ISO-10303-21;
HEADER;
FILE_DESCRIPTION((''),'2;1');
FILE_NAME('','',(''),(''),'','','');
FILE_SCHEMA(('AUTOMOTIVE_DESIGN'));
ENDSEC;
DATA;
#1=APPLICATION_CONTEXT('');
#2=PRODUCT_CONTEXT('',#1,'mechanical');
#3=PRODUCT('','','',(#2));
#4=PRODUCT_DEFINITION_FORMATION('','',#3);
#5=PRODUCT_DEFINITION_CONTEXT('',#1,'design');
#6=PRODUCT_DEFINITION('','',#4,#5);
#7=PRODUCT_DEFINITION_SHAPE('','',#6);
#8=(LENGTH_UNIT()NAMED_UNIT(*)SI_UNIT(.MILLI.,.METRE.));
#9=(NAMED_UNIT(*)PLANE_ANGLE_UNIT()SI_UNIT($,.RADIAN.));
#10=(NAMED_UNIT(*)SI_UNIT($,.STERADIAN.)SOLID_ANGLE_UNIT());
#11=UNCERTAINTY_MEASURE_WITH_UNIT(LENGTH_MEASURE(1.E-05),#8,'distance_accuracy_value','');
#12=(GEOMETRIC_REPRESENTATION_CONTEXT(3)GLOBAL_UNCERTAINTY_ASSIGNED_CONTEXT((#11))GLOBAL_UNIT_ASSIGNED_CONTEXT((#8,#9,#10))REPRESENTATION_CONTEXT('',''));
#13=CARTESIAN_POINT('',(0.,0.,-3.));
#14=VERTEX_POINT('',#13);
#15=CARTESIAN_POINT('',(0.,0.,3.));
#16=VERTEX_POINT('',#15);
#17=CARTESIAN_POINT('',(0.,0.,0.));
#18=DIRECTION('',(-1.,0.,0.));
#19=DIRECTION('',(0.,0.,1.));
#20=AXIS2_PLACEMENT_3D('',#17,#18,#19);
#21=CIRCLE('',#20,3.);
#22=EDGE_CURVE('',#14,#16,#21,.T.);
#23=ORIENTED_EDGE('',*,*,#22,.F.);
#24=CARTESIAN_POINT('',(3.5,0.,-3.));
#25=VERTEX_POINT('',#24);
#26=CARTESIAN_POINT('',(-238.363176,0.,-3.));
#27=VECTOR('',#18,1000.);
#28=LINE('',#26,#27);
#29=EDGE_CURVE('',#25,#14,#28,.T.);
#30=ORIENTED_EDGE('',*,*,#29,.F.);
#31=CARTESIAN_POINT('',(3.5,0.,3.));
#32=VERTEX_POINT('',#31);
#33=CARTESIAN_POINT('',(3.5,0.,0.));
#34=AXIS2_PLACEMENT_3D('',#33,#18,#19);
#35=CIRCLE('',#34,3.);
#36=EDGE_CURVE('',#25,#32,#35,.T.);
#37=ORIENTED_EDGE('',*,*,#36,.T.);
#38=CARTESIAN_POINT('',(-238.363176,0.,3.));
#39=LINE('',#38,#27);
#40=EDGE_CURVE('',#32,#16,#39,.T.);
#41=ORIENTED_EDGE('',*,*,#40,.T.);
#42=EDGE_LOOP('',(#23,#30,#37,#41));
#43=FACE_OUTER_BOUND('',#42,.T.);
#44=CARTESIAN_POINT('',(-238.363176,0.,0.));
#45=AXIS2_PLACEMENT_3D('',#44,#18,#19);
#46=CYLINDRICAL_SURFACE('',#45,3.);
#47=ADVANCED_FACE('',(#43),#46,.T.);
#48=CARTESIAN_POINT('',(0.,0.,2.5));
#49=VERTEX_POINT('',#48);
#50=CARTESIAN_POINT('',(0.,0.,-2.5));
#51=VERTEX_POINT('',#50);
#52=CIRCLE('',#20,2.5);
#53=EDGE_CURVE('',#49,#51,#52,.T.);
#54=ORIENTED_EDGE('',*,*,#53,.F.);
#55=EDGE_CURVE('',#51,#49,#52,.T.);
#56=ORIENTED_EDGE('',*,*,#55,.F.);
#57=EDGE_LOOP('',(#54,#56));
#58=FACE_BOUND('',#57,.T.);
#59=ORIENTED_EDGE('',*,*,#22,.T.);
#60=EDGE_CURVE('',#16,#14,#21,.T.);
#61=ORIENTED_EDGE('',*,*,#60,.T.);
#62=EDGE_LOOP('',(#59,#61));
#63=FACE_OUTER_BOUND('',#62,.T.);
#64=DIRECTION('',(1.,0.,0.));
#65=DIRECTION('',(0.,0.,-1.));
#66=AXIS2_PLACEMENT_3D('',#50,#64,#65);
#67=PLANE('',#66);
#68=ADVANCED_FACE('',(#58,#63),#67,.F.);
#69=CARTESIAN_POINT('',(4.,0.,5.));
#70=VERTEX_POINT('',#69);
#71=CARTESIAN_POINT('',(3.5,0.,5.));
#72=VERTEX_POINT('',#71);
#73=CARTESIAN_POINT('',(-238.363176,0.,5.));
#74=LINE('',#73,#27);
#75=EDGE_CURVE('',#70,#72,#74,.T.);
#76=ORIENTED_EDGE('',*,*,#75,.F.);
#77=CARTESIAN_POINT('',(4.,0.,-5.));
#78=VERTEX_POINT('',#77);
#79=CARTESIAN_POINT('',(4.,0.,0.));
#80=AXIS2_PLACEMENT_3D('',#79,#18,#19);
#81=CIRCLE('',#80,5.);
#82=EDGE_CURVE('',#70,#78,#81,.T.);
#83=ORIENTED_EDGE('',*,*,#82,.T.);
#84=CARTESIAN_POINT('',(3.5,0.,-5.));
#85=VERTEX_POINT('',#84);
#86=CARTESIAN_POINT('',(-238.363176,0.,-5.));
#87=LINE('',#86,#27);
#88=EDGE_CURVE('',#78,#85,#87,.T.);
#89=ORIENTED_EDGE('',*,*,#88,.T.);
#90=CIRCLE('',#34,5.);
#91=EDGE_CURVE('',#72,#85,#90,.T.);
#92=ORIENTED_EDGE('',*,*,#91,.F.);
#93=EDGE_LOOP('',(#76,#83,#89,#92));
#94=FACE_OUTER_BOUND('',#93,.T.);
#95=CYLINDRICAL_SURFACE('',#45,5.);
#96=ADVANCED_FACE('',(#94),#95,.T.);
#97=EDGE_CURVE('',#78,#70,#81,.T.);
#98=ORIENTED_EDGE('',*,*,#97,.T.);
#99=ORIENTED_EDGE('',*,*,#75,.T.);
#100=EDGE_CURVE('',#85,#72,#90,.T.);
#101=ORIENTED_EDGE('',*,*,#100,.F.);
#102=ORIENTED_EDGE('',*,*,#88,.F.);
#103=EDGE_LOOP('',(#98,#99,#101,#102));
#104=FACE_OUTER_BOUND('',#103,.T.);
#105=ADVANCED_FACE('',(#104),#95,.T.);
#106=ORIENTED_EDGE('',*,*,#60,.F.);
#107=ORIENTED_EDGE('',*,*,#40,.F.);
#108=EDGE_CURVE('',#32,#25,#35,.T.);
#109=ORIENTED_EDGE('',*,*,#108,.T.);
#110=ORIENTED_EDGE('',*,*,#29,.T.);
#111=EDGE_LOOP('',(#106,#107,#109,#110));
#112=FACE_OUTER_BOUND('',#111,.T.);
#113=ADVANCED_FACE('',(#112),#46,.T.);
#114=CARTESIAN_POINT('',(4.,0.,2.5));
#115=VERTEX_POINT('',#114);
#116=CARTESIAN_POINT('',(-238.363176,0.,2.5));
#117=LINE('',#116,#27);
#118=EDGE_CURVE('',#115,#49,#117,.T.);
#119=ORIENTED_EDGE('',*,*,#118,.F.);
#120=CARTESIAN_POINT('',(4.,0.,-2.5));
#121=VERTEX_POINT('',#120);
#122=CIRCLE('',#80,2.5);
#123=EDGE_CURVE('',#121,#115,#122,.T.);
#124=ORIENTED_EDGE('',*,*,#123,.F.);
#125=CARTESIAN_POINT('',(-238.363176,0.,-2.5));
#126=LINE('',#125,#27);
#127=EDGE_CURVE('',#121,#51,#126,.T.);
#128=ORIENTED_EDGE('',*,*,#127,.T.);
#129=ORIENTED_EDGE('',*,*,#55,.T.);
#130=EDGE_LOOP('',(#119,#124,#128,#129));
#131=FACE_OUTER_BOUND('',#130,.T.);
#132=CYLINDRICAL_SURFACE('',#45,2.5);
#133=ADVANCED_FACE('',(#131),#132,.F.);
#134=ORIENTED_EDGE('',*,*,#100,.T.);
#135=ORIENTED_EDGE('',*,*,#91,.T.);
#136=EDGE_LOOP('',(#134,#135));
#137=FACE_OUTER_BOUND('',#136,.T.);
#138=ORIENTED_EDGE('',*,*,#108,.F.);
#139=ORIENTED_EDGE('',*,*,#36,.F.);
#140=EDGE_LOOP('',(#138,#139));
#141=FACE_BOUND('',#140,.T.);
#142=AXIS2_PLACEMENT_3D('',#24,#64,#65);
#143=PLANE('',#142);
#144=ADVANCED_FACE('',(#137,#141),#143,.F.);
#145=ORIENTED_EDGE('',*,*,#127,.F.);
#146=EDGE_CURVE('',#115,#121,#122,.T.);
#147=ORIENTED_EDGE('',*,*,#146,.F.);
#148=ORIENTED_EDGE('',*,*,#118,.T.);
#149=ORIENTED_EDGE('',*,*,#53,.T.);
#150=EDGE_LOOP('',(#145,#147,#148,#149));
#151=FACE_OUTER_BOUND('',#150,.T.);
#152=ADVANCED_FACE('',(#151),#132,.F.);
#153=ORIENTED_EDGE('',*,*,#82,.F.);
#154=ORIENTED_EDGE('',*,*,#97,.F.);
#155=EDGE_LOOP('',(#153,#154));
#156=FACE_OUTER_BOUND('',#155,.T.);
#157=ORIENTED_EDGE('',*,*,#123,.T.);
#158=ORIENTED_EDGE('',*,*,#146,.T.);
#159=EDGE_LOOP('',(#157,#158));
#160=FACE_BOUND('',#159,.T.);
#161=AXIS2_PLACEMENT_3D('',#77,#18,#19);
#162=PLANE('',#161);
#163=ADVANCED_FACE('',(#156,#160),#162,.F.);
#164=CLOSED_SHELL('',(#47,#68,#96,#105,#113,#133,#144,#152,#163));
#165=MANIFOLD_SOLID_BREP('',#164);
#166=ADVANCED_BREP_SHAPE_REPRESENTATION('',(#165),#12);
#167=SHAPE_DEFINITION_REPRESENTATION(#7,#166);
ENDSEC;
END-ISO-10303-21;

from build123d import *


with BuildPart() as part:
    # 草图1 → 旋转1 (revolve)
    with BuildSketch(Plane(origin=(0, 0, 0), x_dir=(1, 0, 0), z_dir=(0, 1, 0)), mode=Mode.PRIVATE) as revolve_1_sk:
        Polygon((0, 2.5), (0, 3), (3.5, 3), (3.5, 5), (4, 5), (4, 2.5), align=None)
    revolve(revolve_1_sk.sketch.rotate(Axis((-238.363176029, 0, 0), (1, 0, 0)), 180), axis=Axis((-238.363176029, 0, 0), (1, 0, 0)))


solid = part.part
